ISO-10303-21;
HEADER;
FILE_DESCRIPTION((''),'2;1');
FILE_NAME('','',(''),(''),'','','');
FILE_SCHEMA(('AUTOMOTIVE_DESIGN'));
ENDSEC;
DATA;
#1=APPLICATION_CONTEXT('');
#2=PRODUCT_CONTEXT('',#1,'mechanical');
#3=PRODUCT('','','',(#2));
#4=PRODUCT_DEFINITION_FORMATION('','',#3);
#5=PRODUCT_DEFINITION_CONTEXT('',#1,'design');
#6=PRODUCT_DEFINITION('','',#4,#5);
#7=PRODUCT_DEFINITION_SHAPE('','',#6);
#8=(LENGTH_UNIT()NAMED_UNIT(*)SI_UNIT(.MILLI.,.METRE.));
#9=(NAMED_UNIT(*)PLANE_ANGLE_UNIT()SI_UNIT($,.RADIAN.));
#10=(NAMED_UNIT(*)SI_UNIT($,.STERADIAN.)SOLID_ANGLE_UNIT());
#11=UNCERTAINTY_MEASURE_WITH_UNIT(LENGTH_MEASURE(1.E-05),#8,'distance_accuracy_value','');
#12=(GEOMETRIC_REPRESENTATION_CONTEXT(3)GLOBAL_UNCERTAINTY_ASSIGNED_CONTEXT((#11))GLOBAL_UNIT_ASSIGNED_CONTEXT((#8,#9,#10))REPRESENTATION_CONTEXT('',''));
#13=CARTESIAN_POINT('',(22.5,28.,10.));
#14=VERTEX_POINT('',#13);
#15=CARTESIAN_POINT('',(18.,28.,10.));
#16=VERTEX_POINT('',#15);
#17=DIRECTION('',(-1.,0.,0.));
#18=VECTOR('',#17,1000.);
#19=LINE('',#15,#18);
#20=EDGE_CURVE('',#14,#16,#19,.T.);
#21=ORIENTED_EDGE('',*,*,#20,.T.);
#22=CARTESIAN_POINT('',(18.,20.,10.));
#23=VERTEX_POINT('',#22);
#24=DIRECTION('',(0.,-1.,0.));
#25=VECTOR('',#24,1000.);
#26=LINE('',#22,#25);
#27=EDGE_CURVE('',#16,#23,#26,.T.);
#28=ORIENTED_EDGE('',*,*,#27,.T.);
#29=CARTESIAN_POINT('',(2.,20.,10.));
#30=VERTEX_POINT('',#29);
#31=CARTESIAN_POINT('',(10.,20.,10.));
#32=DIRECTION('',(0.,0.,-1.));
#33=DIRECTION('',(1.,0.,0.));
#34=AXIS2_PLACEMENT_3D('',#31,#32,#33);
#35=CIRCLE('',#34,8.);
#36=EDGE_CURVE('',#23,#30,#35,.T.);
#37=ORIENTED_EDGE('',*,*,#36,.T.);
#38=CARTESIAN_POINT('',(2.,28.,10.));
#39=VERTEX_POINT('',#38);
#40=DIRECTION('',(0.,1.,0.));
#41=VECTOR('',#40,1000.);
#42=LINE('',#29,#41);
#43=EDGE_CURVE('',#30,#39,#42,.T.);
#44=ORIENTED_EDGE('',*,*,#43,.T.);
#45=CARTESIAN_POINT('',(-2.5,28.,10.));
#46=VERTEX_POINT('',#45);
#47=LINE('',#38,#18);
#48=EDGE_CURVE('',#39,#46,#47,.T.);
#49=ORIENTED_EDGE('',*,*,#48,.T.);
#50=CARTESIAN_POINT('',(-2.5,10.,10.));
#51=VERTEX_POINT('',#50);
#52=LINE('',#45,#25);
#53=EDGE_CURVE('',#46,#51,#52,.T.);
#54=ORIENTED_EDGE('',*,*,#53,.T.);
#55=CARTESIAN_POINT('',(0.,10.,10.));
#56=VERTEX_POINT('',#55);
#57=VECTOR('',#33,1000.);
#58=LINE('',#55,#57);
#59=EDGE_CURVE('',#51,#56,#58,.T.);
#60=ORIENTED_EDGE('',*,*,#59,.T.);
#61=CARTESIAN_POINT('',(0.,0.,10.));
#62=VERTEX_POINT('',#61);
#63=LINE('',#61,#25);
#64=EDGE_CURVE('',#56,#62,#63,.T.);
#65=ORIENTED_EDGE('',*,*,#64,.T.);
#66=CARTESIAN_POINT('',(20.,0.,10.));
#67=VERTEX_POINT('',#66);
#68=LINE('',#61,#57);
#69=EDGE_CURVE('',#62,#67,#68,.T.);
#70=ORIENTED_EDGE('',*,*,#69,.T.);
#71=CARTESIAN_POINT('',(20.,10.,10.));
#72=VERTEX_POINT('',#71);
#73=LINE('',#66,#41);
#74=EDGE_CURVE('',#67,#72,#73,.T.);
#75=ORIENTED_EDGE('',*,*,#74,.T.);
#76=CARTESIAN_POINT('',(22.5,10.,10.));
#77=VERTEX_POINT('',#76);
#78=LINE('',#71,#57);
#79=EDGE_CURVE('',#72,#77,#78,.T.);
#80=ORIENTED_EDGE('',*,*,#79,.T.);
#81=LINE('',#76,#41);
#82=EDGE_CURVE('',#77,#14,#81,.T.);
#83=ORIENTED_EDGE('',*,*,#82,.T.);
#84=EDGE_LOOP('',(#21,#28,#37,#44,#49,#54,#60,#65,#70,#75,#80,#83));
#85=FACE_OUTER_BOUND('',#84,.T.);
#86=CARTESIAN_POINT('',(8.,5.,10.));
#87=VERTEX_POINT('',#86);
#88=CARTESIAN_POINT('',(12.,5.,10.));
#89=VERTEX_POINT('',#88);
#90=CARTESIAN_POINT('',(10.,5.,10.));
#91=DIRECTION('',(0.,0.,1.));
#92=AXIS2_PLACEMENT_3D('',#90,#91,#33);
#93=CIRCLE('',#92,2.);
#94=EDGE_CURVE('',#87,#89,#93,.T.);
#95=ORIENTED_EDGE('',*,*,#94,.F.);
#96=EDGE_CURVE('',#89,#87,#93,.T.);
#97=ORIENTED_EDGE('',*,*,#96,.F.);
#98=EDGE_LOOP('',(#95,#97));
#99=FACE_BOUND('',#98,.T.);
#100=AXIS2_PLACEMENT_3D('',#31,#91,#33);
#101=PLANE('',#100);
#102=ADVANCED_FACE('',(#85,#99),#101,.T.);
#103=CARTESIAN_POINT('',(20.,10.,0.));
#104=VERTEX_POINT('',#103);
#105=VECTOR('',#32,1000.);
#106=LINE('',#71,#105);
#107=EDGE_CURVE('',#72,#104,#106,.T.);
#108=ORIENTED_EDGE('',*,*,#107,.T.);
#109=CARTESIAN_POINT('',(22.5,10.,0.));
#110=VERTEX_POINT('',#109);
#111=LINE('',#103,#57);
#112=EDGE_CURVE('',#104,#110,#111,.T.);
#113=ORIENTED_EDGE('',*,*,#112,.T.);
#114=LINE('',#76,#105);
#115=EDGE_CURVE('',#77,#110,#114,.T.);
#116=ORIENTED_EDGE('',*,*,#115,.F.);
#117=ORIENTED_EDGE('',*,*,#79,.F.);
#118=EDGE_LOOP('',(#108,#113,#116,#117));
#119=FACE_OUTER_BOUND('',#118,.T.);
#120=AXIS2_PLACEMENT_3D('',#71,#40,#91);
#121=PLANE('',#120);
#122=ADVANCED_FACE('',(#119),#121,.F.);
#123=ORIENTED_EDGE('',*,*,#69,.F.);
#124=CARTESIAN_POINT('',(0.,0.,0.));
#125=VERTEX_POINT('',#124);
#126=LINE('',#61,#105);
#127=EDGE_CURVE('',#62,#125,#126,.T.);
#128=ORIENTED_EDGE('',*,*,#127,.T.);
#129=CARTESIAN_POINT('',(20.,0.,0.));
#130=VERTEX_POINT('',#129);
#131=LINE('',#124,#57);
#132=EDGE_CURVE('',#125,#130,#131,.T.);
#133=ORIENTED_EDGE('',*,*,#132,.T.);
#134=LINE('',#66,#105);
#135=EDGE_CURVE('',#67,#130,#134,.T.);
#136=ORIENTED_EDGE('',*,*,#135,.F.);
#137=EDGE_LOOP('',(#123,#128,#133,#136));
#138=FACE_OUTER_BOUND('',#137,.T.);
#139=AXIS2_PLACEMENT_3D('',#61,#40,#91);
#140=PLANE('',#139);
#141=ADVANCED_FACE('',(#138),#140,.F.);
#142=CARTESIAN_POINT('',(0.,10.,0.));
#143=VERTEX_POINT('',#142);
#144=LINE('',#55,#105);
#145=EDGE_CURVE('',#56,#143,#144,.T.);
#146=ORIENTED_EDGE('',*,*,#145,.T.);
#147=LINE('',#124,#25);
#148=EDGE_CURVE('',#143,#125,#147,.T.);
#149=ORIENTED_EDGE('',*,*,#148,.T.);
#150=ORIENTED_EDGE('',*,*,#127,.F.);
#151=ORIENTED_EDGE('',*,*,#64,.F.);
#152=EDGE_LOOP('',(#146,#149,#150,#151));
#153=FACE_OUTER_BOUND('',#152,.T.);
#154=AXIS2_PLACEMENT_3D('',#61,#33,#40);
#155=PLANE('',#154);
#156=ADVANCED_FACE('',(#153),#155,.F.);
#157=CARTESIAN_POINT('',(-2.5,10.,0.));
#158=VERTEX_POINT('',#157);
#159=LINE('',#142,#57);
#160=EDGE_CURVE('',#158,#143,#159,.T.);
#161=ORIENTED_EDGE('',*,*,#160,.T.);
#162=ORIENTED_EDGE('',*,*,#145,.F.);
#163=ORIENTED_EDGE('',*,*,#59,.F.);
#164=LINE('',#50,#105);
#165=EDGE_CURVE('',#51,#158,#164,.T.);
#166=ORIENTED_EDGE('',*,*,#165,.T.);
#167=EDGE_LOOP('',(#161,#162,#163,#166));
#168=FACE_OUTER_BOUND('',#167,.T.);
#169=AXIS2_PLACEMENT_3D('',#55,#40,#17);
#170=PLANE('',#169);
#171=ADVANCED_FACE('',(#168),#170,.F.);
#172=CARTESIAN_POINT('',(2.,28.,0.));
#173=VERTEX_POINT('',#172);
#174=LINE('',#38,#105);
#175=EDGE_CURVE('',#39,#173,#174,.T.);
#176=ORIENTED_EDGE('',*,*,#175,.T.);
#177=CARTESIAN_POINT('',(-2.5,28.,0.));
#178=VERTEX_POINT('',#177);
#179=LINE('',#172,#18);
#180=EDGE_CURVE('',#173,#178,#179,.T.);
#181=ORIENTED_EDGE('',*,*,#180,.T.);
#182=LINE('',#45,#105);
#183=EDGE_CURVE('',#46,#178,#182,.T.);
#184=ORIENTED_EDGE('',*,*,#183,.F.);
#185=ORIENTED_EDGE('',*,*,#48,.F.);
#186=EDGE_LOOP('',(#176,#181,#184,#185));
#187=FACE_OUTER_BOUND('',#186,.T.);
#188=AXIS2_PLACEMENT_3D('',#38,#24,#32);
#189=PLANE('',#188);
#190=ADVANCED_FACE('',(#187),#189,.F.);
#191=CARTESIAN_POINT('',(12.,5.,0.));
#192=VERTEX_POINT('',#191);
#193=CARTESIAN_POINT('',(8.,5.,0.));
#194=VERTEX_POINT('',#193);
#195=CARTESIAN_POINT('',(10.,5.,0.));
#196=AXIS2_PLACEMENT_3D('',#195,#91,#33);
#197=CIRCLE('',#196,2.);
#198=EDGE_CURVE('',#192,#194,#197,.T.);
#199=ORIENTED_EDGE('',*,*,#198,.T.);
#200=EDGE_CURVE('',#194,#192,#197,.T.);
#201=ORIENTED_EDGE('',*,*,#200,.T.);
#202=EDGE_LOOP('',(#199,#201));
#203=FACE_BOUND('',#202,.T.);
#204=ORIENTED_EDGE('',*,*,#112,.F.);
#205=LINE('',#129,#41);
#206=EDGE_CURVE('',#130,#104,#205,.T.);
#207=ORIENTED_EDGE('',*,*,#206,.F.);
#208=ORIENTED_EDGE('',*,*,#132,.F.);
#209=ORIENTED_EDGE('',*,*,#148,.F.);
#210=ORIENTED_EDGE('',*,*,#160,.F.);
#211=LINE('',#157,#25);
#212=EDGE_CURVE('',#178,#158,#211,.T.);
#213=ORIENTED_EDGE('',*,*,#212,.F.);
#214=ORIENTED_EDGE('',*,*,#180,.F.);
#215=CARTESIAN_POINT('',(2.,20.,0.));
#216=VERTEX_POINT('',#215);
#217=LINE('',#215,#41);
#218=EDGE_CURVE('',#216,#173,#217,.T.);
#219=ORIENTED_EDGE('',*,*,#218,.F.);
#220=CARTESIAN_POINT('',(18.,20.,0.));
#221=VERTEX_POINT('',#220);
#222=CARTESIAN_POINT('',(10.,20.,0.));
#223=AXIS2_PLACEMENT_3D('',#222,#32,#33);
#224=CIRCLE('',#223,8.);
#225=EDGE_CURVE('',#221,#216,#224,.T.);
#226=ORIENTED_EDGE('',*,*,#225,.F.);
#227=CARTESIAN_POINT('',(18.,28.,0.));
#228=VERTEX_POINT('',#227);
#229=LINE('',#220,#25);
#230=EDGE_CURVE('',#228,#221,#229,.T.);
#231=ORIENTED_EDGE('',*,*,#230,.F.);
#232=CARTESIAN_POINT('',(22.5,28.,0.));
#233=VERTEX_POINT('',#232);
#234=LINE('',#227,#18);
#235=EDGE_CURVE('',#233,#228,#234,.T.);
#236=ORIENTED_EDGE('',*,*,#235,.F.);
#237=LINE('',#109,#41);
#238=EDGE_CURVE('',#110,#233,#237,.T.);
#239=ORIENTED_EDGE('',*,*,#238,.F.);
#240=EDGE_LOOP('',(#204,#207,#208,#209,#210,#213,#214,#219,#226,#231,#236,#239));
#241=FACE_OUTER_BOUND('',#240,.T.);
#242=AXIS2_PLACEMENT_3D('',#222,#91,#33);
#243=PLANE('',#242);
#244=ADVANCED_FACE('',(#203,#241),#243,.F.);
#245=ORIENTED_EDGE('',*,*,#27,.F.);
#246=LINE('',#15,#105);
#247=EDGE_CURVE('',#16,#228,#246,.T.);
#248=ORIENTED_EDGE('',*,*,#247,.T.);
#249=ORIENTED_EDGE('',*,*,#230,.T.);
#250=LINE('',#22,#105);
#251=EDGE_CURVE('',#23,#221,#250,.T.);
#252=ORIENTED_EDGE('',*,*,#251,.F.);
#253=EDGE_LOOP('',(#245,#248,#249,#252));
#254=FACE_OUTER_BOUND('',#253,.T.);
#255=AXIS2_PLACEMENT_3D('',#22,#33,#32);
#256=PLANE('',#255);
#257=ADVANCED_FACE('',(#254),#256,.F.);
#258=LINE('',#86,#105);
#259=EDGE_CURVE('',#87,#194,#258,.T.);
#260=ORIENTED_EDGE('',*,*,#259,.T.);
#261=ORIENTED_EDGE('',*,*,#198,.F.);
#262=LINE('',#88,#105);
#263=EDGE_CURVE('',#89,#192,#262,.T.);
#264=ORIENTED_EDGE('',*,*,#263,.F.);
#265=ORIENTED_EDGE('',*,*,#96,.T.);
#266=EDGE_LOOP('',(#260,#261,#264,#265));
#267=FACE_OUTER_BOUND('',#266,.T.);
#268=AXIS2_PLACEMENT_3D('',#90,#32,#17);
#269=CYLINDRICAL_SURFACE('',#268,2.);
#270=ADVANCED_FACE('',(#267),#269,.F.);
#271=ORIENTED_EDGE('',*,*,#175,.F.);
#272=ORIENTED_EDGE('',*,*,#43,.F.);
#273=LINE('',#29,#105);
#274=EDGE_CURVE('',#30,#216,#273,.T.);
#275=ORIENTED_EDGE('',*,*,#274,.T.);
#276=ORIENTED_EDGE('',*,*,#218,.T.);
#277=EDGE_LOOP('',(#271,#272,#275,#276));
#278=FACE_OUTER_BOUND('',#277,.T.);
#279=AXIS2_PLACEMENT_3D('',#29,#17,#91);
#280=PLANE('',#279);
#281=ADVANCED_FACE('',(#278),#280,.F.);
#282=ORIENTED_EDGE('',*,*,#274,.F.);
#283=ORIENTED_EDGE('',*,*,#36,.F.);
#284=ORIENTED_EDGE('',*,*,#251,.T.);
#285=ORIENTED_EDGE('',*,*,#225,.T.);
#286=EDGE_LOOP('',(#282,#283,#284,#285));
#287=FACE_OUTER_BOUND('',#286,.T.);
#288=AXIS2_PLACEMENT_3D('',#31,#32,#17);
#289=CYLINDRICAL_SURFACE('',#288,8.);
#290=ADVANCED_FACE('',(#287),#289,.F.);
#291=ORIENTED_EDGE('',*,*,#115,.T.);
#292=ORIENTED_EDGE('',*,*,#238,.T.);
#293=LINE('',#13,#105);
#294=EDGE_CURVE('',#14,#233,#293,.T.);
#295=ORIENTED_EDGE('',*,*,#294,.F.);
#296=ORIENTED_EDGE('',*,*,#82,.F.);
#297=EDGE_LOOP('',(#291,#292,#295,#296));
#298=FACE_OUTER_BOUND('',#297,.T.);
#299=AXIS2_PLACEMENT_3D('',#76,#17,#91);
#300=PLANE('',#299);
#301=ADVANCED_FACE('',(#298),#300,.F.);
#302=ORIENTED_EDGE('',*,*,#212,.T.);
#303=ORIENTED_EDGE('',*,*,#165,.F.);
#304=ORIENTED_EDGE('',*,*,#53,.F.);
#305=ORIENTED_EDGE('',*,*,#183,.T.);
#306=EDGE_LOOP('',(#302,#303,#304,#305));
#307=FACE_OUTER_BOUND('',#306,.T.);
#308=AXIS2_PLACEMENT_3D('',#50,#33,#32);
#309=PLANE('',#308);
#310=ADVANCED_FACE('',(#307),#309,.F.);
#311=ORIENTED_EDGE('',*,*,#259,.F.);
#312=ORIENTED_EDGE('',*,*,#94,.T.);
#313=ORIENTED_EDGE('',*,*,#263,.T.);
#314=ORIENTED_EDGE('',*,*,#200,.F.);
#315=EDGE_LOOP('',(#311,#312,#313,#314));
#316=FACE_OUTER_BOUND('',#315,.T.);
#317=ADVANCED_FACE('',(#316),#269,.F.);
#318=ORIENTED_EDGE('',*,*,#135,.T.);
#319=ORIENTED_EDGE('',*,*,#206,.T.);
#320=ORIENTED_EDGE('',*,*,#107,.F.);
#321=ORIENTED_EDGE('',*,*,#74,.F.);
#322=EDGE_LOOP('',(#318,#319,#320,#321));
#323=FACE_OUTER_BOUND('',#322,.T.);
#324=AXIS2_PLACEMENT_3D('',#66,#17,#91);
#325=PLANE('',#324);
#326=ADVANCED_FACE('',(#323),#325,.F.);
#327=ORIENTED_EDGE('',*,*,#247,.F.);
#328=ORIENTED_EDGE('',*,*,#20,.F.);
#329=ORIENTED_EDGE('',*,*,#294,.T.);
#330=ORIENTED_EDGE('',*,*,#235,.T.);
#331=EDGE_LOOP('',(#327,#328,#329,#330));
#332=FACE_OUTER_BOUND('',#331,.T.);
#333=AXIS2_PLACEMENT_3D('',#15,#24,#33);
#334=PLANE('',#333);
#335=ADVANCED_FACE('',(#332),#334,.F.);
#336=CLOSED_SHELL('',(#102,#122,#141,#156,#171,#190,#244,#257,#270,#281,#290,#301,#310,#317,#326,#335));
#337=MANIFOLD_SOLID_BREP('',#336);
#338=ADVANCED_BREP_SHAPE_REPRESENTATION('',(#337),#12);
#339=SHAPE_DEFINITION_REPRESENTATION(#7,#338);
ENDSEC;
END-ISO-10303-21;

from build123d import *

# Parameters (mm, degrees)
SKETCH_1_R      = 2
EXTRUDE_1_DEPTH = 10


with BuildPart() as part:
    # 草图1 → 凸台-拉伸1 (new body)
    with BuildSketch(Plane.XY):
        with BuildLine():
            Line((0, 10), (-2.5, 10))
            Line((-2.5, 10), (-2.5, 27.142110135))
            Line((-2.5, 27.142110135), (-2.5, 28))
            Line((-2.5, 28), (2, 28))
            Line((2, 28), (2, 20))
            ThreePointArc((2, 20), (10, 12), (18, 20))
            Line((18, 20), (18, 28))
            Line((18, 28), (22.5, 28))
            Line((22.5, 28), (22.5, 10))
            Line((22.5, 10), (20, 10))
            Line((20, 10), (20, 0))
            Line((20, 0), (0, 0))
            Line((0, 0), (0, 10))
        make_face()
        with Locations((10, 5)):
            Circle(SKETCH_1_R, mode=Mode.SUBTRACT)
    extrude(amount=EXTRUDE_1_DEPTH)


solid = part.part
